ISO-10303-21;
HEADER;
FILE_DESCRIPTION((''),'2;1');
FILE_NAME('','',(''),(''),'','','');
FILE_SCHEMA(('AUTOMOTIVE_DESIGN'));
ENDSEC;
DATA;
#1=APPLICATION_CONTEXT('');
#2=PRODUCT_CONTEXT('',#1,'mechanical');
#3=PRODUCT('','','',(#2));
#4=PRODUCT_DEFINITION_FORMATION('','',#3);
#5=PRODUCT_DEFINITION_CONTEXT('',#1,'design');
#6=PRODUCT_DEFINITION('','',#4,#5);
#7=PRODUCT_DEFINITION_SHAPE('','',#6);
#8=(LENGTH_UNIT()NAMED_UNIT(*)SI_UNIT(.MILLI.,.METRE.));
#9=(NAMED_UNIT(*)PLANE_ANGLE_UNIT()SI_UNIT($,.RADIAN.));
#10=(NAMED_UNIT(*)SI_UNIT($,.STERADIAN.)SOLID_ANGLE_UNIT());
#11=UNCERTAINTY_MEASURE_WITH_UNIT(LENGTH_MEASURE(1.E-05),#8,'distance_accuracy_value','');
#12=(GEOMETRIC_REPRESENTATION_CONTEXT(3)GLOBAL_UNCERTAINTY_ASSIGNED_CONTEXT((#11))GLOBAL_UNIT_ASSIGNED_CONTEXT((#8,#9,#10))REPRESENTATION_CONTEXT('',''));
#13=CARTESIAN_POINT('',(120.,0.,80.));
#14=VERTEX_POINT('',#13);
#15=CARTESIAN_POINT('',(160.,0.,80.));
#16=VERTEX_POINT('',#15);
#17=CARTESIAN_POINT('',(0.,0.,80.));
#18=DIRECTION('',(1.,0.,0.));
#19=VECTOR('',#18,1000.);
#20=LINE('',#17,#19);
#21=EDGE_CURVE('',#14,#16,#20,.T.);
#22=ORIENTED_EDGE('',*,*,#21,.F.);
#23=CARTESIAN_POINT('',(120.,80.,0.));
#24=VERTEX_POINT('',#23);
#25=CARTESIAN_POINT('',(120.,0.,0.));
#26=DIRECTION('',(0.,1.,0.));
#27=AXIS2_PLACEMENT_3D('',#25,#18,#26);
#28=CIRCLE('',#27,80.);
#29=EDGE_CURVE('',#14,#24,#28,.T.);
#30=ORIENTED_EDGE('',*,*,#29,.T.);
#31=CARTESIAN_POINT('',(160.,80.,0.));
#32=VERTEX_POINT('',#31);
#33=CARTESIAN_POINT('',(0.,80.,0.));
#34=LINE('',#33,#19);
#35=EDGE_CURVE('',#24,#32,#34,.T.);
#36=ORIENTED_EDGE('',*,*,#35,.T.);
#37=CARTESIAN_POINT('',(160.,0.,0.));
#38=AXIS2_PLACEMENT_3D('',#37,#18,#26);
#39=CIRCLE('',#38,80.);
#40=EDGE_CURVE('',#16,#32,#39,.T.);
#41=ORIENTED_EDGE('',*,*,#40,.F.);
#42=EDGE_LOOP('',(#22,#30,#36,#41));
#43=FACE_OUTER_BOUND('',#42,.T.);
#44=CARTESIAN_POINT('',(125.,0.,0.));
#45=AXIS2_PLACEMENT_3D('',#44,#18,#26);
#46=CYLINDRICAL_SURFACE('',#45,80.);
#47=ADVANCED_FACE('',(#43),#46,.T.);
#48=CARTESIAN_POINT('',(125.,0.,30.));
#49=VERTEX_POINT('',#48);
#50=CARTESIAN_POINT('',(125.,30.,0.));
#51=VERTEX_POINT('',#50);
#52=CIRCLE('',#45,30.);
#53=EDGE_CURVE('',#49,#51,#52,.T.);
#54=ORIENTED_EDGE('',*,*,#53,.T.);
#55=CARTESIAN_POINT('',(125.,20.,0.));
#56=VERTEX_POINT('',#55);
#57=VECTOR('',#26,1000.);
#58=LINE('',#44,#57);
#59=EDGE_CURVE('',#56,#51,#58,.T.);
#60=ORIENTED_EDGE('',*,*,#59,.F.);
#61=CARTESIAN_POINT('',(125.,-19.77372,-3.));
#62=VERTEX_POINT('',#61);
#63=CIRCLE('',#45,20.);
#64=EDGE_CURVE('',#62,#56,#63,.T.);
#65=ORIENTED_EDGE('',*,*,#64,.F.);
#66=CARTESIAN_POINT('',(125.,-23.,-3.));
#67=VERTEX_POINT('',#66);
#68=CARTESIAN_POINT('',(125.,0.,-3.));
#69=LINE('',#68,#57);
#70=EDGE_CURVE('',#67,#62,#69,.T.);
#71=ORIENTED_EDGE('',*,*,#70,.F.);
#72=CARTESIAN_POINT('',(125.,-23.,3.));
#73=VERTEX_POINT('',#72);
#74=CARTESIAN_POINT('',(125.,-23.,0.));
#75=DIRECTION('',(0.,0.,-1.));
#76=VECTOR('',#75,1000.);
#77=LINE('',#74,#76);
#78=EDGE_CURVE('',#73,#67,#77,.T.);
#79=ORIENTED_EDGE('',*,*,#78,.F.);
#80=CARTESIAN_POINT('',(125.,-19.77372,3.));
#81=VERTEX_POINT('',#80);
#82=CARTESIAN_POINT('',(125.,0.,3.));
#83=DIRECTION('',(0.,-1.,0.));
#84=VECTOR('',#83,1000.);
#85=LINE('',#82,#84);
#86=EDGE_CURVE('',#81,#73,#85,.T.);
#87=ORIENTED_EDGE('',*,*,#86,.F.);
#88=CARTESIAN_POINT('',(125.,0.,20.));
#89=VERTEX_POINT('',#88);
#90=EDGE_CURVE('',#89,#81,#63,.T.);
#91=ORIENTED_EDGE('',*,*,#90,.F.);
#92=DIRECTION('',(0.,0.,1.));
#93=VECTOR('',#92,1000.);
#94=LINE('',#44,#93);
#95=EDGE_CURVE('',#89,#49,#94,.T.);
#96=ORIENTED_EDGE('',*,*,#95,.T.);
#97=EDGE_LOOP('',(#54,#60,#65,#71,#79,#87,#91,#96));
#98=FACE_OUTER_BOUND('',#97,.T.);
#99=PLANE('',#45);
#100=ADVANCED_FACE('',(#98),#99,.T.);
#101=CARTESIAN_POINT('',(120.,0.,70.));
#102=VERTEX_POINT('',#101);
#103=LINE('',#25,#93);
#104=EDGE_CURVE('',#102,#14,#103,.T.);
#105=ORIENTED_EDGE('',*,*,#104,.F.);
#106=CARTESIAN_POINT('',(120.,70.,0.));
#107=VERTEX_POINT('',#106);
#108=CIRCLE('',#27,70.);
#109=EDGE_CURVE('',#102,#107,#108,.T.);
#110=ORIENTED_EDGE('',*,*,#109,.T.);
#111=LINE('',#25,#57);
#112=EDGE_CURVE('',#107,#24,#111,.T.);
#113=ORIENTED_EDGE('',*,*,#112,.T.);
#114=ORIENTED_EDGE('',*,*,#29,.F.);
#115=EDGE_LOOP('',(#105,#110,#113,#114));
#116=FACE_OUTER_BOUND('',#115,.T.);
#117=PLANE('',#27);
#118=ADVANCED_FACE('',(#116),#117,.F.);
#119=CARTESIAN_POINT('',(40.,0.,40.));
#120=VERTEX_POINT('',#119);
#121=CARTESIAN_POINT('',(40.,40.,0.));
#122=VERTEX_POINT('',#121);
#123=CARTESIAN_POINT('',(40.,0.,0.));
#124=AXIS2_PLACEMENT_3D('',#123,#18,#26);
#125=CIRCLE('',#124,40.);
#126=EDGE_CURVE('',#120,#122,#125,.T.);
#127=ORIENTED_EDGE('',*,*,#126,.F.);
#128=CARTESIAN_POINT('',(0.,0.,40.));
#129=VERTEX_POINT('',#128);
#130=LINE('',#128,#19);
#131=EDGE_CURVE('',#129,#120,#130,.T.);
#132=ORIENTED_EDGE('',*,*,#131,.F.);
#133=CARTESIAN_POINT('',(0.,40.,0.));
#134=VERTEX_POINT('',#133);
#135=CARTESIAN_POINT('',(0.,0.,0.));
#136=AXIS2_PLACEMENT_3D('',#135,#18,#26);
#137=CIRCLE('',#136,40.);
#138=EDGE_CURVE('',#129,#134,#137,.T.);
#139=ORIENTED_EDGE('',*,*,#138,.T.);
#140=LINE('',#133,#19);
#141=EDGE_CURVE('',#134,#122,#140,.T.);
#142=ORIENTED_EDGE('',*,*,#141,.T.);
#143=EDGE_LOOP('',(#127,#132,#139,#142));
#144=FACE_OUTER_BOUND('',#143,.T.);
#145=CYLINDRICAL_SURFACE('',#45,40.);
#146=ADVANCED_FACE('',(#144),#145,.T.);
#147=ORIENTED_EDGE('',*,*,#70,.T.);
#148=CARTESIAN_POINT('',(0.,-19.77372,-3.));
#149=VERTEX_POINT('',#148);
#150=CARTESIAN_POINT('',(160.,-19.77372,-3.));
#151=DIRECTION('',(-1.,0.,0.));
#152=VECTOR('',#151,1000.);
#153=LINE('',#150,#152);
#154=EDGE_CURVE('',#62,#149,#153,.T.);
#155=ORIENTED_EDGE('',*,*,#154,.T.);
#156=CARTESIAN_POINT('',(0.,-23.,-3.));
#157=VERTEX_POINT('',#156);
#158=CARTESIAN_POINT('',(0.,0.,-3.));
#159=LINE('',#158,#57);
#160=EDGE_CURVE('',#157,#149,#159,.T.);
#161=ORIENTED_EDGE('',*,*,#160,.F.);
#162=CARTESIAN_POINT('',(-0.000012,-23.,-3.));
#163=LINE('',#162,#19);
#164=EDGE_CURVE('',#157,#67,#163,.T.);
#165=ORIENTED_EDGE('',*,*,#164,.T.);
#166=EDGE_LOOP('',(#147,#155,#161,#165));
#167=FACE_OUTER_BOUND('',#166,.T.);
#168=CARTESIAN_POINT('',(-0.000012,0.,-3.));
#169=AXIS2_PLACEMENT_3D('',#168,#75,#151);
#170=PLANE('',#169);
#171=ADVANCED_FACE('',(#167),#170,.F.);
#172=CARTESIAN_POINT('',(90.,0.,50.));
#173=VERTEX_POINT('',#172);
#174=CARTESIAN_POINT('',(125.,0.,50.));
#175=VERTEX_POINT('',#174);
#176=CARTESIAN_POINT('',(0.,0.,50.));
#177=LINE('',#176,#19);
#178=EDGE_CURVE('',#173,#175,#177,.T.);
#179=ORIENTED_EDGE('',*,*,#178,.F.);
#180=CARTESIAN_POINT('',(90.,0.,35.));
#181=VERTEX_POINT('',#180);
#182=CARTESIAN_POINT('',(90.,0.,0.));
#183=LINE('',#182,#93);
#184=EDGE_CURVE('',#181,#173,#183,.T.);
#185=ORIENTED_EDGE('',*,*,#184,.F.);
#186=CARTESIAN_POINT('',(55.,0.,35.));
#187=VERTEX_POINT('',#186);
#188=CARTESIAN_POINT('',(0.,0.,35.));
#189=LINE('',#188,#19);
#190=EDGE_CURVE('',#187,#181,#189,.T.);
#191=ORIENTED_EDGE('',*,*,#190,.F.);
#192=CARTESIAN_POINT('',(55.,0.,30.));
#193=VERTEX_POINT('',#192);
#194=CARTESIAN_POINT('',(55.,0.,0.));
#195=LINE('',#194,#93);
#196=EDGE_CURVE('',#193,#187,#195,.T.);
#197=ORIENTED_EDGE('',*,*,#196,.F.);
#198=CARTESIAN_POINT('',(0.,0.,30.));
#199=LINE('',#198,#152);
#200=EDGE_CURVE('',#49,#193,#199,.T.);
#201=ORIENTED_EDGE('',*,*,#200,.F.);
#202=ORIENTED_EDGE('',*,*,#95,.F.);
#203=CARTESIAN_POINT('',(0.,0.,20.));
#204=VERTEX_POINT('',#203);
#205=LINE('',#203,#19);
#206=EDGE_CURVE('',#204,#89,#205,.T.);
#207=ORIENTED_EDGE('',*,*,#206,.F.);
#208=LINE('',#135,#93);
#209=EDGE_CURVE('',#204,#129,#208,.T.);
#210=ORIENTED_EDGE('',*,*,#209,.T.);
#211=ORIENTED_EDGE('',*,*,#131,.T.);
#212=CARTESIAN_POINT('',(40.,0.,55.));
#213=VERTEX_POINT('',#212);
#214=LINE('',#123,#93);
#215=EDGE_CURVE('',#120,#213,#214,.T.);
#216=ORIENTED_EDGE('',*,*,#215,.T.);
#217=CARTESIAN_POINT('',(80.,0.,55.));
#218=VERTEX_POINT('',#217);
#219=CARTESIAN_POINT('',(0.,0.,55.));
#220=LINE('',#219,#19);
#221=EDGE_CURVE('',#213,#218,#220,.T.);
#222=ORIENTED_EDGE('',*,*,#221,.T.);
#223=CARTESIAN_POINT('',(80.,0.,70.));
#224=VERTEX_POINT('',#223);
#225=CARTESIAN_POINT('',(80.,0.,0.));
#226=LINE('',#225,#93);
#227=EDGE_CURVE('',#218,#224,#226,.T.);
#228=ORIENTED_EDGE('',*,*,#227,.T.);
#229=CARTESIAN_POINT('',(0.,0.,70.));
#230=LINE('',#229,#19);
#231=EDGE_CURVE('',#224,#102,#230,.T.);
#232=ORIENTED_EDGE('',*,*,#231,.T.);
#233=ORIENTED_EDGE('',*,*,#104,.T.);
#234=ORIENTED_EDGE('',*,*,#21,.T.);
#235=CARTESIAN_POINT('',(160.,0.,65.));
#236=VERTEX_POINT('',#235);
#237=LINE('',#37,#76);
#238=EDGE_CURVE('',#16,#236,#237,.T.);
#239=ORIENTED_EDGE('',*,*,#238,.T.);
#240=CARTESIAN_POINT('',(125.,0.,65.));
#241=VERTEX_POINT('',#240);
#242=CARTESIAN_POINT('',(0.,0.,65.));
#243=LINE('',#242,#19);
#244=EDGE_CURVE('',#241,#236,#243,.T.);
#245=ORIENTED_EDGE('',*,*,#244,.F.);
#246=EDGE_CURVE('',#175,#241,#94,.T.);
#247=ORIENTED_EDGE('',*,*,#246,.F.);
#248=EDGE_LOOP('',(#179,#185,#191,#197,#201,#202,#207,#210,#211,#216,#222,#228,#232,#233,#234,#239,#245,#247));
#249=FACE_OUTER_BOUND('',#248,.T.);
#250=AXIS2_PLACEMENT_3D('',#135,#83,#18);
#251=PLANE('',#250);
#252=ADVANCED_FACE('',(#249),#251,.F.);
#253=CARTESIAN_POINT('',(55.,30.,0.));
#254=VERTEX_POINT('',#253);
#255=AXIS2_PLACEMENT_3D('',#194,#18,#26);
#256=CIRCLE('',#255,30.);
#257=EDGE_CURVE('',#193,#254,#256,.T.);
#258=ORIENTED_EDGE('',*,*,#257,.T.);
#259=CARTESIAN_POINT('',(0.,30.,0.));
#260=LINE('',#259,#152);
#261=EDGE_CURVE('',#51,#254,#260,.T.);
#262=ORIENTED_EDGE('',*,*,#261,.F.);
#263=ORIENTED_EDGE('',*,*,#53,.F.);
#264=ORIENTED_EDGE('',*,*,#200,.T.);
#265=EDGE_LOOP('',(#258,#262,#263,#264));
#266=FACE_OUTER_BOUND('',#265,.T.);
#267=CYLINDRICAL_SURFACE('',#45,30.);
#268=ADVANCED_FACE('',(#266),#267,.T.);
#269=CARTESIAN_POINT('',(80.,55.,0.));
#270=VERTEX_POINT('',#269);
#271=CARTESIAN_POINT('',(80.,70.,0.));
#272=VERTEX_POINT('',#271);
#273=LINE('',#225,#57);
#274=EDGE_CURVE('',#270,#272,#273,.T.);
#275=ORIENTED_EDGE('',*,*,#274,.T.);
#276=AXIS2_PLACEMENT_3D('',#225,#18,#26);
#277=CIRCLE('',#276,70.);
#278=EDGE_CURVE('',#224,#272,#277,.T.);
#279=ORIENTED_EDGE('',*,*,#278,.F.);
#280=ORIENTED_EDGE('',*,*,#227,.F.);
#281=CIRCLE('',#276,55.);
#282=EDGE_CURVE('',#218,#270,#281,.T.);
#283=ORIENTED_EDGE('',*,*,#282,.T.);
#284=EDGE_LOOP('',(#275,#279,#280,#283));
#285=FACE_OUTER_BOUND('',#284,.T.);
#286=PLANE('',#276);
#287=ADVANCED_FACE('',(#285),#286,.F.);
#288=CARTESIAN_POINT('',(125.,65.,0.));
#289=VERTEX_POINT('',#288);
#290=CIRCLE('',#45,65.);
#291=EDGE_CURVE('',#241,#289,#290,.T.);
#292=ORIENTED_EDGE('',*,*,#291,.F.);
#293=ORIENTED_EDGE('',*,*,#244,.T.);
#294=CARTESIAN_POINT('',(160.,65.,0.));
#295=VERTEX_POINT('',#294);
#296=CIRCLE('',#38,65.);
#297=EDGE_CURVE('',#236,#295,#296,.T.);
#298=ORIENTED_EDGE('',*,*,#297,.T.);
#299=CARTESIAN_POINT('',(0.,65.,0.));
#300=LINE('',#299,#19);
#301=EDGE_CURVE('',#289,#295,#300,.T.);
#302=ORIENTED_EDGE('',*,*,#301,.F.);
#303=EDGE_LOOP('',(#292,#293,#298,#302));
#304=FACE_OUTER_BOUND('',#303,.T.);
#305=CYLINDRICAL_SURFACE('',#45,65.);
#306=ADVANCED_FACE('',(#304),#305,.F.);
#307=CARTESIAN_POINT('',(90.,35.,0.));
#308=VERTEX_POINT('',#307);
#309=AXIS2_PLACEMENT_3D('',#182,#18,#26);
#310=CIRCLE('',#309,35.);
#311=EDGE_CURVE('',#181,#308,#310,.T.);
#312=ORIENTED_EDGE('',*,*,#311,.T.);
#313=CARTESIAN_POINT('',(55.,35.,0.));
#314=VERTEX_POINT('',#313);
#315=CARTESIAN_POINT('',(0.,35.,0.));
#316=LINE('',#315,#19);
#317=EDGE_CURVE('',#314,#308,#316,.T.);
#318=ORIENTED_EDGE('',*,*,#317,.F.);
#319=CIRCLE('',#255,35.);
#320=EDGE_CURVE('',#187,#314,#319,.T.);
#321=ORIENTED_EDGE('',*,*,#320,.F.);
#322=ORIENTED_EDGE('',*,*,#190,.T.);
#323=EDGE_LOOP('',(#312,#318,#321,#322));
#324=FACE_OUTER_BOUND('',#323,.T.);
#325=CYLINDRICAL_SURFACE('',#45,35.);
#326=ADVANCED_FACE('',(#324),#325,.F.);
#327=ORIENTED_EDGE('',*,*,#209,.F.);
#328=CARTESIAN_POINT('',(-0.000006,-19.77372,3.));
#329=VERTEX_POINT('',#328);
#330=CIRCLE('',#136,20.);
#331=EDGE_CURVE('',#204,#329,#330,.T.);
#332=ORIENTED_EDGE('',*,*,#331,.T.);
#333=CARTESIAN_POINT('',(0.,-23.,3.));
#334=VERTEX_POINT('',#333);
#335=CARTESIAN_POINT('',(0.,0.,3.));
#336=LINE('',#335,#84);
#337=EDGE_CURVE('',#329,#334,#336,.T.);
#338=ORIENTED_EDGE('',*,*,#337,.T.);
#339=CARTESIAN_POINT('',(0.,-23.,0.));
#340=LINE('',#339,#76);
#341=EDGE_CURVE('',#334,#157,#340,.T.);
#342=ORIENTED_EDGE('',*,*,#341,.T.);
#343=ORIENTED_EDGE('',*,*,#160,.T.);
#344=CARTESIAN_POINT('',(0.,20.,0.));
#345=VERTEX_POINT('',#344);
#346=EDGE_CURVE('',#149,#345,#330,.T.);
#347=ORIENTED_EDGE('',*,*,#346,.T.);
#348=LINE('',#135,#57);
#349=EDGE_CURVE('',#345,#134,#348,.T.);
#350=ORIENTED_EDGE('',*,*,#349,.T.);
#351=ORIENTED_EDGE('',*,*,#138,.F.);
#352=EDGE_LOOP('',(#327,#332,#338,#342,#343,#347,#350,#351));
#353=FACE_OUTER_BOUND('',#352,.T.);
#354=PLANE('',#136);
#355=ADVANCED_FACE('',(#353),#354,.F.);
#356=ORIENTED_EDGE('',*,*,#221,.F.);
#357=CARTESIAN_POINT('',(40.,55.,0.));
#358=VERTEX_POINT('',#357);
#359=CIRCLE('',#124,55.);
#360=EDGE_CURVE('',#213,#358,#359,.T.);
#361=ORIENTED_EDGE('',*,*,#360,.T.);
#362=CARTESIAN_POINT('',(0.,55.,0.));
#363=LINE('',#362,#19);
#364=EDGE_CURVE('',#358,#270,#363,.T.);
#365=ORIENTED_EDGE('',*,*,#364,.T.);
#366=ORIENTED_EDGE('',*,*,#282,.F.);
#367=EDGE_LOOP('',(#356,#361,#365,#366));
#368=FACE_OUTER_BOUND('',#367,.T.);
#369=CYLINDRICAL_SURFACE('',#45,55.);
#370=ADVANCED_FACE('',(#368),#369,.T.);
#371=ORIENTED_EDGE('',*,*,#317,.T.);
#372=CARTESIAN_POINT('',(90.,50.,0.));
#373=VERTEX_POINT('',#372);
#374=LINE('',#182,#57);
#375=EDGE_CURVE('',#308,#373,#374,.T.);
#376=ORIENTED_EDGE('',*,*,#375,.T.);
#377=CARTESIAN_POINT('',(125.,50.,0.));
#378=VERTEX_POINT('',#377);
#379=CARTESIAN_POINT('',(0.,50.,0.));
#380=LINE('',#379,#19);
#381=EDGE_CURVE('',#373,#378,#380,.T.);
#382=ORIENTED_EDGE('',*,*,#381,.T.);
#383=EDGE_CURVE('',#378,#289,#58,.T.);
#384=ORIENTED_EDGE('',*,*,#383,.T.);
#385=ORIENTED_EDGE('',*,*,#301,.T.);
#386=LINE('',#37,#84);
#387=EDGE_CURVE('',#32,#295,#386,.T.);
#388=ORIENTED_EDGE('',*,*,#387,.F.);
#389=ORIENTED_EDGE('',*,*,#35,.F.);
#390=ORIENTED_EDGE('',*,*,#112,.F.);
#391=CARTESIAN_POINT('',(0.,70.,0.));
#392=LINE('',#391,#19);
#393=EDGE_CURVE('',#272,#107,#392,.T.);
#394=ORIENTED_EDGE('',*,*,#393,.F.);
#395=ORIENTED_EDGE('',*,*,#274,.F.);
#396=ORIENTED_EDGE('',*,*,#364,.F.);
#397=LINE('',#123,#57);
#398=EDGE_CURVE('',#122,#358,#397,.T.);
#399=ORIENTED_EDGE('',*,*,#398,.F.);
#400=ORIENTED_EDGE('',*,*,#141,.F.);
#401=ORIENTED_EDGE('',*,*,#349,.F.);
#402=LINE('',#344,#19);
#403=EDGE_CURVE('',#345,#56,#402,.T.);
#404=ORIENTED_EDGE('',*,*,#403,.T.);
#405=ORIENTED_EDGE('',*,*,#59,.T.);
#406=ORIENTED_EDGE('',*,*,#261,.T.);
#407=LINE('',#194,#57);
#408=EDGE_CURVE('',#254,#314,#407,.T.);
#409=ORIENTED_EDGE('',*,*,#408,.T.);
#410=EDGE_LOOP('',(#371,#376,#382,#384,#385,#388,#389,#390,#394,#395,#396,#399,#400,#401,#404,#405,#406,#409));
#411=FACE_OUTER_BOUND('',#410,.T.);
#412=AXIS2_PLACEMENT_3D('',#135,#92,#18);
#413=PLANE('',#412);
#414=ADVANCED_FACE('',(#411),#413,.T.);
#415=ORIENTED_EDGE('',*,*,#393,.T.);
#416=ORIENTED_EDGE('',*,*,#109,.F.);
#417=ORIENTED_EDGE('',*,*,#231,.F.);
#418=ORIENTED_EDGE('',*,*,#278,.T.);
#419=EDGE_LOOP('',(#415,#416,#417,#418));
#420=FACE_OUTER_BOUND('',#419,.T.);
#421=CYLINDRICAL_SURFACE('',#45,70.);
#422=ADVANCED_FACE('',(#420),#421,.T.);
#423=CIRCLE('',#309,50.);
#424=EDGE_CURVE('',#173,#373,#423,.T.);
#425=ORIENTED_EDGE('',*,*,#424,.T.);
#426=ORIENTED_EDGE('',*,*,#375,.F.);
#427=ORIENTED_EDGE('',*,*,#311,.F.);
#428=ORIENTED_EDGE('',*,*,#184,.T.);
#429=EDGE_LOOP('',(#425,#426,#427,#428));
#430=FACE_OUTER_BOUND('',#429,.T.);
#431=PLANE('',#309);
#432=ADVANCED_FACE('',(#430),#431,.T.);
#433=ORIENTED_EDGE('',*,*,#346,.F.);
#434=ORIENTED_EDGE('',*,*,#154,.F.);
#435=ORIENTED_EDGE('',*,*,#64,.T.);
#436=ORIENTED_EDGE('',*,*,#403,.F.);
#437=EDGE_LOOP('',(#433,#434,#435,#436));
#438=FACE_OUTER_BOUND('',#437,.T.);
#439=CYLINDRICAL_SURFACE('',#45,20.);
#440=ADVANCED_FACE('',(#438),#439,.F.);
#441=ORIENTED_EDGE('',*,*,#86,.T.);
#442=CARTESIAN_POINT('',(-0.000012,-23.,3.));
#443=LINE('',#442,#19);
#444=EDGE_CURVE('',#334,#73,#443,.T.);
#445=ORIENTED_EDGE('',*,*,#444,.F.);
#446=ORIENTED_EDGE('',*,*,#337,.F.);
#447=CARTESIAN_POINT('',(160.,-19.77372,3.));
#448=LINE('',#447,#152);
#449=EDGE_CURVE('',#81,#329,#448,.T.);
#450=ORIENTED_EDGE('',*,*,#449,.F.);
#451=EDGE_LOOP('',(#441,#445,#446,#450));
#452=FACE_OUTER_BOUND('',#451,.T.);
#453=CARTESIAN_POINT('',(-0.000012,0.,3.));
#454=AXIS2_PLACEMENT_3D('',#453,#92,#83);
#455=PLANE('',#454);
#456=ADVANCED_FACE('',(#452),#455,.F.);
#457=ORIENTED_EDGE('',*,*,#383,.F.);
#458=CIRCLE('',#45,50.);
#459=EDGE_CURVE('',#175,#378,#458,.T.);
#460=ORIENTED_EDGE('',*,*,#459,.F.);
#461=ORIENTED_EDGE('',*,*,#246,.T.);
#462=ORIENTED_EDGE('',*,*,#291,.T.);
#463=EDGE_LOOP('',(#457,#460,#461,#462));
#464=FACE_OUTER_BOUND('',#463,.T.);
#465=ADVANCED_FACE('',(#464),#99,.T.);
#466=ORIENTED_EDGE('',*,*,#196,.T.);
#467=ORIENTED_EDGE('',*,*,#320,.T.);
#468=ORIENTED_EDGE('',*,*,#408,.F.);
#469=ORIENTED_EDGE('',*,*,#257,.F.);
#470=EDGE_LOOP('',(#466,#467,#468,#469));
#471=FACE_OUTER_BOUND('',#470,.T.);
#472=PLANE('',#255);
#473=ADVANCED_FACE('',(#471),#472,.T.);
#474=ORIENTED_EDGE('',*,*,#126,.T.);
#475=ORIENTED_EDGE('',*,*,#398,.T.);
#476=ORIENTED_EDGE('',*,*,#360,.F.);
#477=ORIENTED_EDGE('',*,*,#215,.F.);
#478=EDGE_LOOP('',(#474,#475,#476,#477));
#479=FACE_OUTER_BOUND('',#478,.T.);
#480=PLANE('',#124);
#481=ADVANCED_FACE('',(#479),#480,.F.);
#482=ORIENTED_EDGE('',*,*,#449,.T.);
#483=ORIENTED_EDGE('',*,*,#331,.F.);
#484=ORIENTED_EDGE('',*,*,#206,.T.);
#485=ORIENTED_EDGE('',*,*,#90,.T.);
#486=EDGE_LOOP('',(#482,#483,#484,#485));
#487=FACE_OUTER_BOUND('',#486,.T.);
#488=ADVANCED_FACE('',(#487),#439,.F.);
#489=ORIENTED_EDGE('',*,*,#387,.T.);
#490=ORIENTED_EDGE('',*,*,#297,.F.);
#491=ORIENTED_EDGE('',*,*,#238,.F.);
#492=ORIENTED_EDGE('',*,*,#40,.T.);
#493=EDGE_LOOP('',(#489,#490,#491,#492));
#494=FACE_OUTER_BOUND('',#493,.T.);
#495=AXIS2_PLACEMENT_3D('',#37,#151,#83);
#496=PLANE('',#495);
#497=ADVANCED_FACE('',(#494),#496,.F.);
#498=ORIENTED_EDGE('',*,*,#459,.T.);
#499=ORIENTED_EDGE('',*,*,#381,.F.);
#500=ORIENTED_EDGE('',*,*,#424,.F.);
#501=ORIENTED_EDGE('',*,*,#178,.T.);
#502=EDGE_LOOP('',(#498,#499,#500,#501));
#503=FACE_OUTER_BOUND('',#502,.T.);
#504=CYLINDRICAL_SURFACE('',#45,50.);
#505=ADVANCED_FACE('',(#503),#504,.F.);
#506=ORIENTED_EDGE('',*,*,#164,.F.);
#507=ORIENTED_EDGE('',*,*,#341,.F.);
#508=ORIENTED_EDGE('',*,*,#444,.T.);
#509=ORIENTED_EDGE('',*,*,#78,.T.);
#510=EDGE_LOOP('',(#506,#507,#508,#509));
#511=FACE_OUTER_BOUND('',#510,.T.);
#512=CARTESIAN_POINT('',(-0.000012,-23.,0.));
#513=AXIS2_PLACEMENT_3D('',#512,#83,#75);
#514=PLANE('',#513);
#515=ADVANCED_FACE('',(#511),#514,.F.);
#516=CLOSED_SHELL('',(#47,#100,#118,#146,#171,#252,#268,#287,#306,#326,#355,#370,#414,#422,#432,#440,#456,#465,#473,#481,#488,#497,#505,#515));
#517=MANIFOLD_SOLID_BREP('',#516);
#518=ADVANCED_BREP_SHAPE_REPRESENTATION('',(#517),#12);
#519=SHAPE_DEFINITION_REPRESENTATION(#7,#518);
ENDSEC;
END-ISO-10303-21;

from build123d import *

# Parameters (mm, degrees)
STEPPED_PULLEY_BODY_ANGLE  = 270
KEYWAY_SLOT_6X3_DEPTH      = 196.959179423
KEYWAY_SLOT_6X3_DEPTH_BACK = 196.959179423


with BuildPart() as part:
    # Pulley Profile Sketch → Stepped Pulley Body (revolve)
    with BuildSketch(Plane.XY):
        Polygon((0, 40), (0, 20), (125, 20), (125, 30), (55, 30), (55, 35), (90, 35), (90, 50), (125, 50), (125, 65), (160, 65), (160, 80), (120, 80), (120, 70), (80, 70), (80, 55), (40, 55), (40, 40), align=None)
    revolve(axis=Axis((125, 0, 0), (-1, 0, 0)), revolution_arc=STEPPED_PULLEY_BODY_ANGLE)

    # Keyway Slot Sketch → Keyway Slot 6x3 (cut, two sides: drawn at the far end of the back side and taken through both)
    with BuildSketch(Plane(origin=(0, 0, 0), x_dir=(0, 0, -1), z_dir=(1, 0, 0)).offset(-KEYWAY_SLOT_6X3_DEPTH_BACK)):
        with BuildLine():
            ThreePointArc((3, -19.773719933), (1.504260837, -19.943349752), (0, -20))
            Line((0, -20), (0, -23))
            Line((0, -23), (3, -23))
            Line((3, -23), (3, -19.773719933))
        make_face()
        with BuildLine():
            Line((0, -23), (0, -20))
            ThreePointArc((0, -20), (-1.504260837, -19.943349752), (-3, -19.773719933))
            Line((-3, -19.773719933), (-3, -23))
            Line((-3, -23), (0, -23))
        make_face()
    extrude(amount=KEYWAY_SLOT_6X3_DEPTH + KEYWAY_SLOT_6X3_DEPTH_BACK, mode=Mode.SUBTRACT)


solid = part.part
